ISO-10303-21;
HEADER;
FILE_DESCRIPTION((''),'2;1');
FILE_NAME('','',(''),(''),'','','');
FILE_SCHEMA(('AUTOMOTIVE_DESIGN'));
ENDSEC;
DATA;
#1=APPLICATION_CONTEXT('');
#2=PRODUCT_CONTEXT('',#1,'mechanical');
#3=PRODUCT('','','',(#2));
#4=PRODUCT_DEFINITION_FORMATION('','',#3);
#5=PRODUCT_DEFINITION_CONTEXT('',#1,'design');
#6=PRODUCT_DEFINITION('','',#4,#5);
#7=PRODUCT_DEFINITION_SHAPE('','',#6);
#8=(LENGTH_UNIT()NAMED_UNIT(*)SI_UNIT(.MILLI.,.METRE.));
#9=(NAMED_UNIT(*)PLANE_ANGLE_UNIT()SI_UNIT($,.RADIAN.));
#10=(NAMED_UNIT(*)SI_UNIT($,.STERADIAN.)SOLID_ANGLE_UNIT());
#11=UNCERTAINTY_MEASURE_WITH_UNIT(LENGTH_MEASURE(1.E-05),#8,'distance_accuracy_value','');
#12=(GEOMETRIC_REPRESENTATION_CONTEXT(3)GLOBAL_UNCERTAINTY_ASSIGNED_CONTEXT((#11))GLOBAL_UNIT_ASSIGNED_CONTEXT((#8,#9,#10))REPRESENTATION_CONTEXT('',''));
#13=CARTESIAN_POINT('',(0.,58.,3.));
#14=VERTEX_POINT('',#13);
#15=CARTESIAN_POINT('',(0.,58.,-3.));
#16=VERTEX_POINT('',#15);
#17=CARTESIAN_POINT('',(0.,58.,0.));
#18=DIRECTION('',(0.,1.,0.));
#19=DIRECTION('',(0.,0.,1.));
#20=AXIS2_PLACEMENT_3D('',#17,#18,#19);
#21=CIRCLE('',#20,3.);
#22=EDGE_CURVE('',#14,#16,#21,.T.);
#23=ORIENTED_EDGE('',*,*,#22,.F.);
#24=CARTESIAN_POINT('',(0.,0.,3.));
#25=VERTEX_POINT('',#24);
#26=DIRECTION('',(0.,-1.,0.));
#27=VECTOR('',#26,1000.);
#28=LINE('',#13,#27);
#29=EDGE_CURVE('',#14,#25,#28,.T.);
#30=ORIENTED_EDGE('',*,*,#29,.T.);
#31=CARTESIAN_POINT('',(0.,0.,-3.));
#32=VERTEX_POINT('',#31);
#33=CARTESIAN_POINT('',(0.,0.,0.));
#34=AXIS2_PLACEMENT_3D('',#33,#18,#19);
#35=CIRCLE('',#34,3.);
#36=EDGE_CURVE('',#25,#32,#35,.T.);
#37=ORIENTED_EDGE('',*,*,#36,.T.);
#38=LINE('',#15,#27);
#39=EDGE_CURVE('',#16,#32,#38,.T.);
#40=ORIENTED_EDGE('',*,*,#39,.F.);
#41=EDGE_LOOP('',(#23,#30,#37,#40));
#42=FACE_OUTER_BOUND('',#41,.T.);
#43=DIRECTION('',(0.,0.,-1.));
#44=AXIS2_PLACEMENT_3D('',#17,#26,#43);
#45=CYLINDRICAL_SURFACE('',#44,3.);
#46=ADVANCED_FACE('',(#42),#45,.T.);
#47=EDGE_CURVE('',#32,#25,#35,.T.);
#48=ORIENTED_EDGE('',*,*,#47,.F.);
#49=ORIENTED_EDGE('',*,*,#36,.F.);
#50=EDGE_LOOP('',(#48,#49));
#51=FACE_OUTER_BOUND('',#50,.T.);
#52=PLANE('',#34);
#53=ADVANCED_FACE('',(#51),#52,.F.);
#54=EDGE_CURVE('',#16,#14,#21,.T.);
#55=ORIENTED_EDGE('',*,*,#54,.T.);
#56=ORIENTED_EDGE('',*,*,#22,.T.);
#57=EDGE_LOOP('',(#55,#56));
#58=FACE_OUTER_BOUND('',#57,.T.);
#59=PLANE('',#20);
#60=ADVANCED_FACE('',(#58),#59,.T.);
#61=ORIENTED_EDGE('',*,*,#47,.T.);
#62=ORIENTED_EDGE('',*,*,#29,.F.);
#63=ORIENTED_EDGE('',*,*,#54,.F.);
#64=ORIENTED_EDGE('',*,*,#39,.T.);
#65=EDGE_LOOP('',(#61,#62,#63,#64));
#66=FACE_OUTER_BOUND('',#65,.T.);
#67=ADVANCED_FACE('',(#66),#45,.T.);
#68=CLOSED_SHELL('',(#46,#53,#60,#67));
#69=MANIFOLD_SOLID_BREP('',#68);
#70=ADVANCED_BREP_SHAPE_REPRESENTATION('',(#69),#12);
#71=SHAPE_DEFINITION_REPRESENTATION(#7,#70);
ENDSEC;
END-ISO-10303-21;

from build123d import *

# Parameters (mm, degrees)
SKETCH_1_R      = 3
SKETCH_1_R_2    = 1.5
EXTRUDE_1_DEPTH = 58


with BuildPart() as part:
    # 草图1 → 凸台-拉伸1 (new body)
    # profile 1 of 2: a face of its own
    with BuildSketch(Plane(origin=(0, 0, 0), x_dir=(1, 0, 0), z_dir=(0, 1, 0))):
        with Locations(Location((0, 0, 0), (0, 0, 90))):
            Circle(SKETCH_1_R)
        Circle(SKETCH_1_R_2, mode=Mode.SUBTRACT)
    # profile 2 of 2: a face of its own
    with BuildSketch(Plane(origin=(0, 0, 0), x_dir=(1, 0, 0), z_dir=(0, 1, 0))):
        Circle(SKETCH_1_R_2)
    extrude(amount=EXTRUDE_1_DEPTH)


solid = part.part
